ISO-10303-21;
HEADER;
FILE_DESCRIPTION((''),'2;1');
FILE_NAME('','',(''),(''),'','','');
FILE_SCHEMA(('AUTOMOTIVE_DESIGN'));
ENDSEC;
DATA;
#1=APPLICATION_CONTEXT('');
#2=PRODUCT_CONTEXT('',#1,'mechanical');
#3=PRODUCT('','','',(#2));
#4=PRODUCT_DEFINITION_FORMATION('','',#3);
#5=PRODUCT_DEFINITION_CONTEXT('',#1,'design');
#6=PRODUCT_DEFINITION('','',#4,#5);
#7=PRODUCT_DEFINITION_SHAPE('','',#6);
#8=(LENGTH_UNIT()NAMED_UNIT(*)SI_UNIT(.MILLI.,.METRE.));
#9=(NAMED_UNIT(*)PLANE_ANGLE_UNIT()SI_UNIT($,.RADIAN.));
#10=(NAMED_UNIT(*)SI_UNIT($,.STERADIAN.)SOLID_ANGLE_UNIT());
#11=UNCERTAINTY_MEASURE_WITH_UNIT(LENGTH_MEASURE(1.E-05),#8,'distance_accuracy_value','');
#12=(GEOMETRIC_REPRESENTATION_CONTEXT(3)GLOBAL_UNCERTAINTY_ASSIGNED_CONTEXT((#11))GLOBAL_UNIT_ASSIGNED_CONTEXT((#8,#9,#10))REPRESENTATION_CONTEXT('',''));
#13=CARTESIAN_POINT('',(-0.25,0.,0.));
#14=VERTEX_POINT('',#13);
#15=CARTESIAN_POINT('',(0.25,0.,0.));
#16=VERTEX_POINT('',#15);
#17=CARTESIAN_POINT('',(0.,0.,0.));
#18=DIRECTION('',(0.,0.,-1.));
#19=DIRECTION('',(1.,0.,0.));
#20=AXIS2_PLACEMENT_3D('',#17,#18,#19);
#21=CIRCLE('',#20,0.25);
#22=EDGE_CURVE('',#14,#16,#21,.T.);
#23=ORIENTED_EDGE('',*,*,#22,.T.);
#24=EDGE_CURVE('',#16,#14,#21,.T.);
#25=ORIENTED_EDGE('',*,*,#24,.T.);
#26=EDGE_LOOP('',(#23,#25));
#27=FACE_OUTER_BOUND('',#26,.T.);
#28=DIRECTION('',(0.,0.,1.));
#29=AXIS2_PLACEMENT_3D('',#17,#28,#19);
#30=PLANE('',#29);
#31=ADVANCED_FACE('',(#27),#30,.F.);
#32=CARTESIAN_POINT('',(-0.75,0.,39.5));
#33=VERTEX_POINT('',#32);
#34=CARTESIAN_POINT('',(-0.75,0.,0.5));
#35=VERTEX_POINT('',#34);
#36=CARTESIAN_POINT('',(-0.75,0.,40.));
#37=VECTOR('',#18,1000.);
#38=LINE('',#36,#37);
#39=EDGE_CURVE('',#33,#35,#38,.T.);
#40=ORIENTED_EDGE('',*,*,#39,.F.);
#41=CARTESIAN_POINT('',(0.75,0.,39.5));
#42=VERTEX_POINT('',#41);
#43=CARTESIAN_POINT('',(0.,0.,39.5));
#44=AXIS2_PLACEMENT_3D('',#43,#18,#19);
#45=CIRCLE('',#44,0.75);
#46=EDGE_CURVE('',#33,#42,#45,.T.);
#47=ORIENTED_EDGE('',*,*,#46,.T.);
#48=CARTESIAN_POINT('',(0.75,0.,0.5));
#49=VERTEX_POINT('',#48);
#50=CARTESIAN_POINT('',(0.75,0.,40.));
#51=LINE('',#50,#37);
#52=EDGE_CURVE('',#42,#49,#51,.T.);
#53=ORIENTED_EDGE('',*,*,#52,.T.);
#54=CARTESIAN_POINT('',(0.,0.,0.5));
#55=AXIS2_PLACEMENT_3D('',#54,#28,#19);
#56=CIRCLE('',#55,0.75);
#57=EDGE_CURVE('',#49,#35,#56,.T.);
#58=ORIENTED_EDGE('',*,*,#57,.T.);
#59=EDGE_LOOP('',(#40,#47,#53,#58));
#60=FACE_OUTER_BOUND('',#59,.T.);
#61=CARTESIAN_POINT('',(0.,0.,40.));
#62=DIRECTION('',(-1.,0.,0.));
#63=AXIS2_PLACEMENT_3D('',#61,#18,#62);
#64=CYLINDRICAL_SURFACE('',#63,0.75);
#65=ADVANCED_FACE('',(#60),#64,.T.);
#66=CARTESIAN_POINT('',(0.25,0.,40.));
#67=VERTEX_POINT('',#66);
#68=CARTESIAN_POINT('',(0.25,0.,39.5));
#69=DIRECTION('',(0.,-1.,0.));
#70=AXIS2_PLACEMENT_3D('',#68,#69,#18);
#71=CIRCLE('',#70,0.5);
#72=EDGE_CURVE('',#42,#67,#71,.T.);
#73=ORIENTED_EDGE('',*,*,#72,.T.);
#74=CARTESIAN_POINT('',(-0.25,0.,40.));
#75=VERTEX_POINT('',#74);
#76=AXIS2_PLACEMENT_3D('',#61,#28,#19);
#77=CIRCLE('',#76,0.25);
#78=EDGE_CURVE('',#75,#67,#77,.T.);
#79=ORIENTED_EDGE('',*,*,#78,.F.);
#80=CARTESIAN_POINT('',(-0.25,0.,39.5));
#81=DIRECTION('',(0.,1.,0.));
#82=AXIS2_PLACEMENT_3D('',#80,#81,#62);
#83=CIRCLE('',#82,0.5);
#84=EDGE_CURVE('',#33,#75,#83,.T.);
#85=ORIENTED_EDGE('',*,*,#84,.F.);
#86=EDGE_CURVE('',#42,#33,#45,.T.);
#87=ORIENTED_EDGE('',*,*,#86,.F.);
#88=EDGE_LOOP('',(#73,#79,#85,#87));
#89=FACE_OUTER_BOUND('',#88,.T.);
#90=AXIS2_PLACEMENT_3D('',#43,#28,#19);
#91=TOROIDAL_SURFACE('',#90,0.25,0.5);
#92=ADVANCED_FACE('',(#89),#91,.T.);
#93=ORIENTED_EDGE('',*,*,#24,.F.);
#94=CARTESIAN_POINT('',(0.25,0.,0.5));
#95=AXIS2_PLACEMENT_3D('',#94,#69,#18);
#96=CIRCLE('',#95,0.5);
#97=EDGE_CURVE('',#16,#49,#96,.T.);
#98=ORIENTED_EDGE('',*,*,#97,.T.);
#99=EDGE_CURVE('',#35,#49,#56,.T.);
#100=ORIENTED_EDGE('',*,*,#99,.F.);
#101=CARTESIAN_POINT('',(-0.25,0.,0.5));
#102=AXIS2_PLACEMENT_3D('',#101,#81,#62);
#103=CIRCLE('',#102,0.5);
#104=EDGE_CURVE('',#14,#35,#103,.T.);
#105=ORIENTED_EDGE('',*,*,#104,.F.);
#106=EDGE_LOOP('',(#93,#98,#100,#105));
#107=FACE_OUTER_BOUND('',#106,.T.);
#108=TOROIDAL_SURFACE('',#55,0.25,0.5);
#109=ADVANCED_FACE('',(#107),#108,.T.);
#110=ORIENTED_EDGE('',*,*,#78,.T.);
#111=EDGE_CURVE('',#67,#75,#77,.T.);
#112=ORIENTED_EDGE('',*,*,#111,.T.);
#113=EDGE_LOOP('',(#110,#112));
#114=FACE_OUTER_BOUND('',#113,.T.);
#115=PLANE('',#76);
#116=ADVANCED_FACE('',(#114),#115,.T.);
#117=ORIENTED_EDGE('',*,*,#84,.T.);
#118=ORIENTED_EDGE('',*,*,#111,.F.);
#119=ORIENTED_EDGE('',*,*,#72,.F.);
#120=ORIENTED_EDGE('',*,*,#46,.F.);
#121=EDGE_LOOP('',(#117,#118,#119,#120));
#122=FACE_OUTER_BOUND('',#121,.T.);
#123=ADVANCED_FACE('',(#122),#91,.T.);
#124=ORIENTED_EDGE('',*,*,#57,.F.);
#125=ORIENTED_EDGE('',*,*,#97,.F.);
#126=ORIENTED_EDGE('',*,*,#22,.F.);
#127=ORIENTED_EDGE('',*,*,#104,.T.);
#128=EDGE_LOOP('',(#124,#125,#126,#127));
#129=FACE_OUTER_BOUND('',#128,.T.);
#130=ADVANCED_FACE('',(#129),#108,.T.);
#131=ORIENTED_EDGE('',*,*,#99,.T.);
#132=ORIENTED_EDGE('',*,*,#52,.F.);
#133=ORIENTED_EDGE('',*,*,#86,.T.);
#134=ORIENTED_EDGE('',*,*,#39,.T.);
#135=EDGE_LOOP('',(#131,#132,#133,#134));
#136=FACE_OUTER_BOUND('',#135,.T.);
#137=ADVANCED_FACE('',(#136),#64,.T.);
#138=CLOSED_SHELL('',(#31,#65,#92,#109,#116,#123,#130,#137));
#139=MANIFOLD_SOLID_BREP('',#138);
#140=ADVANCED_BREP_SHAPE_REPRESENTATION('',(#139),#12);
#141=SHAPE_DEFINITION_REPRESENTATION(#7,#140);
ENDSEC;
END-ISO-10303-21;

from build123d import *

# Parameters (mm, degrees)
SKETCH1_R           = 0.75
BOSS_EXTRUDE1_DEPTH = 40
FILLET1_R           = 0.5


with BuildPart() as part:
    # Sketch1 → Boss-Extrude1 (new body)
    with BuildSketch(Plane.XY):
        Circle(SKETCH1_R)
    extrude(amount=BOSS_EXTRUDE1_DEPTH)

    # Fillet1
    fillet1_edges = [part.edges().sort_by_distance(p)[0] for p in [
        (-0.75, 0, 0),
        (-0.75, 0, 40),
    ]]
    fillet(fillet1_edges, radius=FILLET1_R)


solid = part.part
